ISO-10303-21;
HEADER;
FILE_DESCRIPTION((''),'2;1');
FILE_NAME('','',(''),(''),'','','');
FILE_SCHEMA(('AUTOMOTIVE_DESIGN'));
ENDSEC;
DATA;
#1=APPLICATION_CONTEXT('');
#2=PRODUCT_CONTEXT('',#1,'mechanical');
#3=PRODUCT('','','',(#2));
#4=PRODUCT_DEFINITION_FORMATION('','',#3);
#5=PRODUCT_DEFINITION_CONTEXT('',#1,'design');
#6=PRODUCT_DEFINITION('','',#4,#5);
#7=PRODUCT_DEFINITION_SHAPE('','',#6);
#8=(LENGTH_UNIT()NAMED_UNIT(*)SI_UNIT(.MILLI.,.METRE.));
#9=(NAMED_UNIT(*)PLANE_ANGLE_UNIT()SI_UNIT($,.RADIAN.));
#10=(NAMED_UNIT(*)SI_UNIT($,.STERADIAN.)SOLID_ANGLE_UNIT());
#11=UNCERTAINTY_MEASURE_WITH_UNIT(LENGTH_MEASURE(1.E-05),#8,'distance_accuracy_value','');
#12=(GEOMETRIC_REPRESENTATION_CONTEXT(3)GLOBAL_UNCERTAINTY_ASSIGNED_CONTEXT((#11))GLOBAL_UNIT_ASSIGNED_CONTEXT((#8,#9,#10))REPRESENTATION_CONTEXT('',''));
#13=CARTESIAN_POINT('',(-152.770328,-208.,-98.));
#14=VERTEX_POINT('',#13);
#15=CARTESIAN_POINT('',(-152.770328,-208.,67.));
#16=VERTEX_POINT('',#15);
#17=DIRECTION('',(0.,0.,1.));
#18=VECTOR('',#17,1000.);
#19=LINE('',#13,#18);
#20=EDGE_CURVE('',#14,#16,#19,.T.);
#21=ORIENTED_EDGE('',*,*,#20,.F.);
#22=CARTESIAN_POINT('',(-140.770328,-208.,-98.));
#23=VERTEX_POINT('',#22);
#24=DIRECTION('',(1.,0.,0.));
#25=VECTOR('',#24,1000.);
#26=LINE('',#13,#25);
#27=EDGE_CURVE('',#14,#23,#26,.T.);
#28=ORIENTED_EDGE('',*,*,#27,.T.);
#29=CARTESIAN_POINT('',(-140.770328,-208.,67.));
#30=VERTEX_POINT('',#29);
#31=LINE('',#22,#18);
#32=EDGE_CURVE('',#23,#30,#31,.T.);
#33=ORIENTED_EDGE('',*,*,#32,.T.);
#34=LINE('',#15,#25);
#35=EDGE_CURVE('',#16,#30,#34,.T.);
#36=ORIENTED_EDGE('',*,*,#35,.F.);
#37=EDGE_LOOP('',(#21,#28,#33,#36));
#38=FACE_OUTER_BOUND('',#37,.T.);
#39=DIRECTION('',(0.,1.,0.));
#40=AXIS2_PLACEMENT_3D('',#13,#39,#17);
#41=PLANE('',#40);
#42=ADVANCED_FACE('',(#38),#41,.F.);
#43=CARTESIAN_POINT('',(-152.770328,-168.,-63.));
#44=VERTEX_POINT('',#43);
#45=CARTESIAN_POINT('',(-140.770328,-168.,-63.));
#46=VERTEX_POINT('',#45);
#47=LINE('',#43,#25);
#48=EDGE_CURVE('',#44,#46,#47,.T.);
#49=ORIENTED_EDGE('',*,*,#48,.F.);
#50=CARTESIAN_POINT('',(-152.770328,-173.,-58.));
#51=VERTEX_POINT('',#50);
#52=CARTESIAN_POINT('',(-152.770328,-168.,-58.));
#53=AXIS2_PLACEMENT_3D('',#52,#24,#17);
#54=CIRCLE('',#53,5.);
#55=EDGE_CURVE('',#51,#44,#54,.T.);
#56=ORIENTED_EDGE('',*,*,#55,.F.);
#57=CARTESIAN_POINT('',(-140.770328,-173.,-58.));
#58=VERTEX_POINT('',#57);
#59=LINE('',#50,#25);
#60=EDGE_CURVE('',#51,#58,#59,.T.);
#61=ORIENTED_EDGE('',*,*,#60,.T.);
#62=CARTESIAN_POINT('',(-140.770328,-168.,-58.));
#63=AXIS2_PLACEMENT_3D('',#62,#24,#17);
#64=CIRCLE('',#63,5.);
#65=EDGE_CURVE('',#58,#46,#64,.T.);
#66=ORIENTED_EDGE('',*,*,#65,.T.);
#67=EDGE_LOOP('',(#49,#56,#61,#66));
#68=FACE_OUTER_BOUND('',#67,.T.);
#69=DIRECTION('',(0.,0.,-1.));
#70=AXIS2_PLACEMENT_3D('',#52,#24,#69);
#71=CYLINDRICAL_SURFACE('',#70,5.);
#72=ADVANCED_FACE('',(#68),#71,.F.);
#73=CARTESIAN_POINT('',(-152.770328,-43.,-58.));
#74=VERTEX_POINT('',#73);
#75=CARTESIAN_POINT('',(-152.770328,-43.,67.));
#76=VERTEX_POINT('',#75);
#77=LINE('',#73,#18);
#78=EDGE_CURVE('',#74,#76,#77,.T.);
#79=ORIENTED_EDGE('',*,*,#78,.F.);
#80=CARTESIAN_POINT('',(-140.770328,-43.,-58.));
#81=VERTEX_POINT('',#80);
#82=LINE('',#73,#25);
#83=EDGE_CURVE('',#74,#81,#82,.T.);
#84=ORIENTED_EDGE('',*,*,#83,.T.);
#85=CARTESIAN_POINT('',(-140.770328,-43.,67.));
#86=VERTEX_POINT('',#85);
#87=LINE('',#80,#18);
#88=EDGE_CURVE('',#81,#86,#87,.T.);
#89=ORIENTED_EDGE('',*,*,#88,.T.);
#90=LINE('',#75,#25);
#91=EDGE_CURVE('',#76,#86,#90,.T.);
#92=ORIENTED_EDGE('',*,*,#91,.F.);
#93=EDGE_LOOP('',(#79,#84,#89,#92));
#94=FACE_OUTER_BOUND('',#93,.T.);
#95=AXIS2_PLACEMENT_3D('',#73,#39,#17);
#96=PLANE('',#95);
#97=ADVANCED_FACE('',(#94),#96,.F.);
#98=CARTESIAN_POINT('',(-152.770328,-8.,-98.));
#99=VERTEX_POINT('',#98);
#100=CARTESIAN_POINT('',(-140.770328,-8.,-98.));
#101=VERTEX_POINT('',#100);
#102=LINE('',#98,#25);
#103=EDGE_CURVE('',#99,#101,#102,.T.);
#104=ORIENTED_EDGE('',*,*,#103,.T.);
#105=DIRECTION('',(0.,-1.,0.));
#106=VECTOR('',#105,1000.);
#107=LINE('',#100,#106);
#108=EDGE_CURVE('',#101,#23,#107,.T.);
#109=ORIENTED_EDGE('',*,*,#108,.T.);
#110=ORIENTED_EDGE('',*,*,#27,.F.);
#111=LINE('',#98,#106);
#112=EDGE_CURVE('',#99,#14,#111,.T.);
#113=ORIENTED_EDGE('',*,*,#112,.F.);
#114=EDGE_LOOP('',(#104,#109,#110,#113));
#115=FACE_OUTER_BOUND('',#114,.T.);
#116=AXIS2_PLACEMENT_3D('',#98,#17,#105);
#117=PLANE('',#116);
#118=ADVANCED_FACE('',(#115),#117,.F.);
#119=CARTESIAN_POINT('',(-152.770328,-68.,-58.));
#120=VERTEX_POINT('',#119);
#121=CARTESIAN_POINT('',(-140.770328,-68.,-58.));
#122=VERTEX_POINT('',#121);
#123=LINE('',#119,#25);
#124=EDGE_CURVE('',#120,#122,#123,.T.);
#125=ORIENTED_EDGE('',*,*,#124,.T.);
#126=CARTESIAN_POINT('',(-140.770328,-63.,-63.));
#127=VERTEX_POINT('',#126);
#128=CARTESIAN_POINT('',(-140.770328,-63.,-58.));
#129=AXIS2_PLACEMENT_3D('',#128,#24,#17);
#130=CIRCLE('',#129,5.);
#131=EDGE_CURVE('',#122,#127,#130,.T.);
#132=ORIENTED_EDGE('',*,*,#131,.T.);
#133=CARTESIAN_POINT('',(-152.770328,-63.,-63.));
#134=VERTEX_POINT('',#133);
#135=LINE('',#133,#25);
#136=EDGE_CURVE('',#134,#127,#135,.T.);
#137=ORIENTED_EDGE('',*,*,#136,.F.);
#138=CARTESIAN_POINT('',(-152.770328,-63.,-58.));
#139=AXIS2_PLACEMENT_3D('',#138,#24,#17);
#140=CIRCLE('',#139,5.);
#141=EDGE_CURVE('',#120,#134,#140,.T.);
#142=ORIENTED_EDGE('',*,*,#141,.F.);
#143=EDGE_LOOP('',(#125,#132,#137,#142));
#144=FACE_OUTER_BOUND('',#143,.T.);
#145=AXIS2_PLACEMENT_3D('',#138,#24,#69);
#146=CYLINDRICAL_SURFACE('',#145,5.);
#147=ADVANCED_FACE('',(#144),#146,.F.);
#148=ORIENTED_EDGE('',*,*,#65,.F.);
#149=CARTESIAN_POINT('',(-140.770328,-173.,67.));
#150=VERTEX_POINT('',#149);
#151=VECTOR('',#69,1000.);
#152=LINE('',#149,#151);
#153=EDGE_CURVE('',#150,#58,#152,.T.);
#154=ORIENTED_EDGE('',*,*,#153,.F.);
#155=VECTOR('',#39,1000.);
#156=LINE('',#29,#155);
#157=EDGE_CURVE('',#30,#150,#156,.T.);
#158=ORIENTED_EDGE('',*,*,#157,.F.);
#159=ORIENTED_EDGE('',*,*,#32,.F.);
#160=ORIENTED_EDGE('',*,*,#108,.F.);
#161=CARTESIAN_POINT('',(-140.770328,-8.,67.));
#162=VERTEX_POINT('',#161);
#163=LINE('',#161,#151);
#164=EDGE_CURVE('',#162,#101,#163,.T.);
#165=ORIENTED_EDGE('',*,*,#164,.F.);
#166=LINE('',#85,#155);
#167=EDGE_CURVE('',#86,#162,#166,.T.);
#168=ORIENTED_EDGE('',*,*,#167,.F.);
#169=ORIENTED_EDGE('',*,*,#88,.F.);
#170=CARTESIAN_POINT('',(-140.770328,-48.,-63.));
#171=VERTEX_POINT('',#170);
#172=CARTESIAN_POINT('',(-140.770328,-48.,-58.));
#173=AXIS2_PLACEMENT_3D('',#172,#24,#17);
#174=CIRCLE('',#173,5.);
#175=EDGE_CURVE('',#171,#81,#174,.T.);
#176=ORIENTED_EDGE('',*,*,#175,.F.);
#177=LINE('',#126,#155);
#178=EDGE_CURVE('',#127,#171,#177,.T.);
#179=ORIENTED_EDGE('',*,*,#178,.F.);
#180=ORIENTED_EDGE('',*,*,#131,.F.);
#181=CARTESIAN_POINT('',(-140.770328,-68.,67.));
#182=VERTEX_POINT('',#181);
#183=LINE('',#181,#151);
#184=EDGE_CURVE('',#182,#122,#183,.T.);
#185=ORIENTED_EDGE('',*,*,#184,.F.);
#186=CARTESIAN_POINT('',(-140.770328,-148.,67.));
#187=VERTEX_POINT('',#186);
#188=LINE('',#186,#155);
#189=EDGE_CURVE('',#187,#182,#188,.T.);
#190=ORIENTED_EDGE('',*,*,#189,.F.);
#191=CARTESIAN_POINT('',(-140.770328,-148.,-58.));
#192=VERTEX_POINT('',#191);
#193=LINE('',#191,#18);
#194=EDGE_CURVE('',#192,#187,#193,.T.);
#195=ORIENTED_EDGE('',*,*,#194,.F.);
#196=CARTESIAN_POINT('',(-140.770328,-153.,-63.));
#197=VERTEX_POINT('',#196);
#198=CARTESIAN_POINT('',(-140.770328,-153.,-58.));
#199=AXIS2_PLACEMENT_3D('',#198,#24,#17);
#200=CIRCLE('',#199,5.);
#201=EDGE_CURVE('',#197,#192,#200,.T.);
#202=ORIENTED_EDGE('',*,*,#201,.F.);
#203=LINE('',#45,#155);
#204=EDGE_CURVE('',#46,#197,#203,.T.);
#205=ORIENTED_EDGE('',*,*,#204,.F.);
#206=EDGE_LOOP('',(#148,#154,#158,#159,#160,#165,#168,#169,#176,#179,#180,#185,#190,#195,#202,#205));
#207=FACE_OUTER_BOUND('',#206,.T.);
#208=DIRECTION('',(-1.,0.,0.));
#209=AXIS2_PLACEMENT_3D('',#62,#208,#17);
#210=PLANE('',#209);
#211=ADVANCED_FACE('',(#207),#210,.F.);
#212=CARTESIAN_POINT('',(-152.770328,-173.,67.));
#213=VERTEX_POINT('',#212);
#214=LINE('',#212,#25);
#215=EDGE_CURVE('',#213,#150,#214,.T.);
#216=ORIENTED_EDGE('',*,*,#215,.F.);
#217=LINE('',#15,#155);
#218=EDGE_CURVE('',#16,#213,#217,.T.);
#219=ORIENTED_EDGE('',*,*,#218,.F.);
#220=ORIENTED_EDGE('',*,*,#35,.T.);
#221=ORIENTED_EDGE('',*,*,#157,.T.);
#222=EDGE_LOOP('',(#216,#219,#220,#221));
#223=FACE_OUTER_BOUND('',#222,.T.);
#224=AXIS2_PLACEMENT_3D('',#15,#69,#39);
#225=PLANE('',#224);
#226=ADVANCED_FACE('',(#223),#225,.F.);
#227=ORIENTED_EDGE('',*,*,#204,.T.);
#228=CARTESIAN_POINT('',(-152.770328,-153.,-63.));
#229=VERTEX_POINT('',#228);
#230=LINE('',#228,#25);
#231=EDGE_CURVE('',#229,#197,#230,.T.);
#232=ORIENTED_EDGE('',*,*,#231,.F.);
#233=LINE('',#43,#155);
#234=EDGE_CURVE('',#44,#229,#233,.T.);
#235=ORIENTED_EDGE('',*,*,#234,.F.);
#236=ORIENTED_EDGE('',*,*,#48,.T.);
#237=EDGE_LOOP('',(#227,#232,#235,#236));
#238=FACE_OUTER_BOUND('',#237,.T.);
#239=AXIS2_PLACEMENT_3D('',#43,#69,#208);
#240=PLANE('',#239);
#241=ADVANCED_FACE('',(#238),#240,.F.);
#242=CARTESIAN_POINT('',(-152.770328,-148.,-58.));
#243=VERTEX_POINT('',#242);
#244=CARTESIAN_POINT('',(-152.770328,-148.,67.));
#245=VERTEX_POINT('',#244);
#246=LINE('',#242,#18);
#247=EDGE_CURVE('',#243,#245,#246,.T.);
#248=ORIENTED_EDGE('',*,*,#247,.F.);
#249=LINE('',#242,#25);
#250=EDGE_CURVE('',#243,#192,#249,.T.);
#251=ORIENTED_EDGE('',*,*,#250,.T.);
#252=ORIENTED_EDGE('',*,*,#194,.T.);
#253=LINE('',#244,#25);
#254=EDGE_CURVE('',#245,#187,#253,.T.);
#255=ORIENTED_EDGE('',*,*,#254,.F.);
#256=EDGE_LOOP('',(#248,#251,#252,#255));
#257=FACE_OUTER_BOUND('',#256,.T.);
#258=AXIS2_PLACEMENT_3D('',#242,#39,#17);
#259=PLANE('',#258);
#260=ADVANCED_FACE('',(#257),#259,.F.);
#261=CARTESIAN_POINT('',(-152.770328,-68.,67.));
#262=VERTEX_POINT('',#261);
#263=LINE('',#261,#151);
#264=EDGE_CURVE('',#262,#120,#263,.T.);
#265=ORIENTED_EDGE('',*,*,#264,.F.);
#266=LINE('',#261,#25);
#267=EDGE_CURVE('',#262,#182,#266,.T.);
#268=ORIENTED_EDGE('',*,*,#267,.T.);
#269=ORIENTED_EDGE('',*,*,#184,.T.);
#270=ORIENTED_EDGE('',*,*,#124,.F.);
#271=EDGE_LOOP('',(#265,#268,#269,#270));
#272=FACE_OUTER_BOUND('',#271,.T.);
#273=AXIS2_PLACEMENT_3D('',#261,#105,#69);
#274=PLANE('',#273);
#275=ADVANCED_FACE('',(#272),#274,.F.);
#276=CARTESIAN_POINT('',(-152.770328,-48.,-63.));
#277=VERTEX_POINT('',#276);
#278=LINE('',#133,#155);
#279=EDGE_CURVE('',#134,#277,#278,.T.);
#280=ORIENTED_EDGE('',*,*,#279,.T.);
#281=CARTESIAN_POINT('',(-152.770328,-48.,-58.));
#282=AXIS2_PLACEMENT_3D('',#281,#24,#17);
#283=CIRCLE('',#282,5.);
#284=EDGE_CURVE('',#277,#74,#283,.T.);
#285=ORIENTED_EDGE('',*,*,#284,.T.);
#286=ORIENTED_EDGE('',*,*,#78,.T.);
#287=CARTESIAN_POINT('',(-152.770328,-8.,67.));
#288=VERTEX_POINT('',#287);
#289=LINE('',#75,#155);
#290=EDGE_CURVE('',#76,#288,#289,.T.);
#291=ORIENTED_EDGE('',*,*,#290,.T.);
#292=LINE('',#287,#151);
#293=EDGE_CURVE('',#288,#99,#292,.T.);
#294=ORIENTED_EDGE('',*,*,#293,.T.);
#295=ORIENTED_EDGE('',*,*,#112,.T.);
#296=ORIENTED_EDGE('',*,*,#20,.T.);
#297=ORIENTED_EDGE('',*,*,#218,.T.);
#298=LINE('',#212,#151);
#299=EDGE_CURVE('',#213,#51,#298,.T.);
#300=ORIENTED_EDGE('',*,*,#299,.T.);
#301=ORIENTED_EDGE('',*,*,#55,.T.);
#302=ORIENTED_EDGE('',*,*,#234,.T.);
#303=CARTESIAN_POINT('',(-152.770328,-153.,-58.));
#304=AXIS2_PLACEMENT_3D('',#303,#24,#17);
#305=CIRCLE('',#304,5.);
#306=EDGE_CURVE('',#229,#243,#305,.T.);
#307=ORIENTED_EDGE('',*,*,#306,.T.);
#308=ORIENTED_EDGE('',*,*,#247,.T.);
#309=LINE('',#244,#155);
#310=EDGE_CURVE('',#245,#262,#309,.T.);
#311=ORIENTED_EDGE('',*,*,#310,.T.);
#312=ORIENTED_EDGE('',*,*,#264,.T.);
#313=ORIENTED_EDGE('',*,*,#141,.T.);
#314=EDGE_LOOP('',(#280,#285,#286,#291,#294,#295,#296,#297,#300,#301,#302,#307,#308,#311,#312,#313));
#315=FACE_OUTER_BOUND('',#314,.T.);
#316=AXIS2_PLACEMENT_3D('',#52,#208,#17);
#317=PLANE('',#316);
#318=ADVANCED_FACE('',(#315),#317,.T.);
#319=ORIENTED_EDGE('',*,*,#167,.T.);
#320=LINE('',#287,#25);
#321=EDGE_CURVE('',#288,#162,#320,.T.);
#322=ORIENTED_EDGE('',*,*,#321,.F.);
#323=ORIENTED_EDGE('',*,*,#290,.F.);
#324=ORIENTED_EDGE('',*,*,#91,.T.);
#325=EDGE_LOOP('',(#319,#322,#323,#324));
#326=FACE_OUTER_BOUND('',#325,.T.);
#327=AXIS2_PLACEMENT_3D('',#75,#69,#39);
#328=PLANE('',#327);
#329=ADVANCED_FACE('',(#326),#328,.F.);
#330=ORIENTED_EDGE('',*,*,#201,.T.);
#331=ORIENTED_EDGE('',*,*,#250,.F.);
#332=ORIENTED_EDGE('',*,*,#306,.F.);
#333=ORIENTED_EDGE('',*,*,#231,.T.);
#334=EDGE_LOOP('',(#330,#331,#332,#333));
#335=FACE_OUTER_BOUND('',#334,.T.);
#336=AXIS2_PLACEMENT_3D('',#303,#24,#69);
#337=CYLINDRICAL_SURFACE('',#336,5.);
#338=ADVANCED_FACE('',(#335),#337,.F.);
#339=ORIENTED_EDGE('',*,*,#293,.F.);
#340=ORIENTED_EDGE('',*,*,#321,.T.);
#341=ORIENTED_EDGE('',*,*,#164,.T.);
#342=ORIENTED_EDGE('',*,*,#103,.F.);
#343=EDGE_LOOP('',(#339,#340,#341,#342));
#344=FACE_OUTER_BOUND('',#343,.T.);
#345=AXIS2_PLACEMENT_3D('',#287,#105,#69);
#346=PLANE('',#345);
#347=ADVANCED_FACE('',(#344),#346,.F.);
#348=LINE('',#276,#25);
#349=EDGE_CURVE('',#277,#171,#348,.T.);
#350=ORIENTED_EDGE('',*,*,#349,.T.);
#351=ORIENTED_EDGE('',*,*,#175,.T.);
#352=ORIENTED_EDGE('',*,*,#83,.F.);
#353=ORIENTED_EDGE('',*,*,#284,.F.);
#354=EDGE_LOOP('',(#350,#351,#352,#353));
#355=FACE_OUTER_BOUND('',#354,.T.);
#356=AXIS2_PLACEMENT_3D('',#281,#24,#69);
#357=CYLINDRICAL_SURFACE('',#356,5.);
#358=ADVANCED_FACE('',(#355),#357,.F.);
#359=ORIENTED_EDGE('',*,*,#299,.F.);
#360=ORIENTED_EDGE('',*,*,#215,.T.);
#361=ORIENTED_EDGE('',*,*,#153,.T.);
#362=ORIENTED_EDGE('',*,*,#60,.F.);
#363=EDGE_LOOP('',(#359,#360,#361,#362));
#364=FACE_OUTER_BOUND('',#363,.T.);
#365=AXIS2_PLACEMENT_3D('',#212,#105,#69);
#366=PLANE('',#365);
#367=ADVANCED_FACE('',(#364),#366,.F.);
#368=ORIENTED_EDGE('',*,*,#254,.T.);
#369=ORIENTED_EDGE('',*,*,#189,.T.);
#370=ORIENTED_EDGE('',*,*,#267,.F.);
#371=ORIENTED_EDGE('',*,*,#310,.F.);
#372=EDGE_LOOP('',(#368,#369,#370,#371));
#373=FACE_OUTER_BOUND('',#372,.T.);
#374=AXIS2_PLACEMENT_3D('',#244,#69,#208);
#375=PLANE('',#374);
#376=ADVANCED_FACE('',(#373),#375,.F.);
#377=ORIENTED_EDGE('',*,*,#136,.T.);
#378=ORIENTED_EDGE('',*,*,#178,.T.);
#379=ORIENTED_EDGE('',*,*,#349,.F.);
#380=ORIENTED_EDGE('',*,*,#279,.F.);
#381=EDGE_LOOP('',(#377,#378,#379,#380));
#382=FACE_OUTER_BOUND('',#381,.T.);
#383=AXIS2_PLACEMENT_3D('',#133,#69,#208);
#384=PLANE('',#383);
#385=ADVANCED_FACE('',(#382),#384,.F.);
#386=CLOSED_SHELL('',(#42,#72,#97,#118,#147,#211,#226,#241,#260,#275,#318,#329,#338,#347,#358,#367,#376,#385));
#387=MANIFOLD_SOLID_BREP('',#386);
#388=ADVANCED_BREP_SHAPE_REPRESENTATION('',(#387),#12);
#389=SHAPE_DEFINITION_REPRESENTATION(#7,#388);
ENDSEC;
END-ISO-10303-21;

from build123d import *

# Parameters (mm, degrees)
EXTRUDE_1_DEPTH = 12


with BuildPart() as part:
    # 草图2 → 凸台-拉伸1 (new body)
    with BuildSketch(Plane.ZY.offset(140.770328303)):
        with BuildLine():
            Line((-63, -168), (-63, -153))
            ThreePointArc((-63, -153), (-61.535533906, -149.464466094), (-58, -148))
            Line((-58, -148), (67, -148))
            Line((67, -148), (67, -68))
            Line((67, -68), (-58, -68))
            ThreePointArc((-58, -68), (-61.535533906, -66.535533906), (-63, -63))
            Line((-63, -63), (-63, -48))
            ThreePointArc((-63, -48), (-61.535533906, -44.464466094), (-58, -43))
            Line((-58, -43), (67, -43))
            Line((67, -43), (67, -8))
            Line((67, -8), (-98, -8))
            Line((-98, -8), (-98, -208))
            Line((-98, -208), (67, -208))
            Line((67, -208), (67, -173))
            Line((67, -173), (-58, -173))
            ThreePointArc((-58, -173), (-61.535533906, -171.535533906), (-63, -168))
        make_face()
    extrude(amount=EXTRUDE_1_DEPTH)


solid = part.part
